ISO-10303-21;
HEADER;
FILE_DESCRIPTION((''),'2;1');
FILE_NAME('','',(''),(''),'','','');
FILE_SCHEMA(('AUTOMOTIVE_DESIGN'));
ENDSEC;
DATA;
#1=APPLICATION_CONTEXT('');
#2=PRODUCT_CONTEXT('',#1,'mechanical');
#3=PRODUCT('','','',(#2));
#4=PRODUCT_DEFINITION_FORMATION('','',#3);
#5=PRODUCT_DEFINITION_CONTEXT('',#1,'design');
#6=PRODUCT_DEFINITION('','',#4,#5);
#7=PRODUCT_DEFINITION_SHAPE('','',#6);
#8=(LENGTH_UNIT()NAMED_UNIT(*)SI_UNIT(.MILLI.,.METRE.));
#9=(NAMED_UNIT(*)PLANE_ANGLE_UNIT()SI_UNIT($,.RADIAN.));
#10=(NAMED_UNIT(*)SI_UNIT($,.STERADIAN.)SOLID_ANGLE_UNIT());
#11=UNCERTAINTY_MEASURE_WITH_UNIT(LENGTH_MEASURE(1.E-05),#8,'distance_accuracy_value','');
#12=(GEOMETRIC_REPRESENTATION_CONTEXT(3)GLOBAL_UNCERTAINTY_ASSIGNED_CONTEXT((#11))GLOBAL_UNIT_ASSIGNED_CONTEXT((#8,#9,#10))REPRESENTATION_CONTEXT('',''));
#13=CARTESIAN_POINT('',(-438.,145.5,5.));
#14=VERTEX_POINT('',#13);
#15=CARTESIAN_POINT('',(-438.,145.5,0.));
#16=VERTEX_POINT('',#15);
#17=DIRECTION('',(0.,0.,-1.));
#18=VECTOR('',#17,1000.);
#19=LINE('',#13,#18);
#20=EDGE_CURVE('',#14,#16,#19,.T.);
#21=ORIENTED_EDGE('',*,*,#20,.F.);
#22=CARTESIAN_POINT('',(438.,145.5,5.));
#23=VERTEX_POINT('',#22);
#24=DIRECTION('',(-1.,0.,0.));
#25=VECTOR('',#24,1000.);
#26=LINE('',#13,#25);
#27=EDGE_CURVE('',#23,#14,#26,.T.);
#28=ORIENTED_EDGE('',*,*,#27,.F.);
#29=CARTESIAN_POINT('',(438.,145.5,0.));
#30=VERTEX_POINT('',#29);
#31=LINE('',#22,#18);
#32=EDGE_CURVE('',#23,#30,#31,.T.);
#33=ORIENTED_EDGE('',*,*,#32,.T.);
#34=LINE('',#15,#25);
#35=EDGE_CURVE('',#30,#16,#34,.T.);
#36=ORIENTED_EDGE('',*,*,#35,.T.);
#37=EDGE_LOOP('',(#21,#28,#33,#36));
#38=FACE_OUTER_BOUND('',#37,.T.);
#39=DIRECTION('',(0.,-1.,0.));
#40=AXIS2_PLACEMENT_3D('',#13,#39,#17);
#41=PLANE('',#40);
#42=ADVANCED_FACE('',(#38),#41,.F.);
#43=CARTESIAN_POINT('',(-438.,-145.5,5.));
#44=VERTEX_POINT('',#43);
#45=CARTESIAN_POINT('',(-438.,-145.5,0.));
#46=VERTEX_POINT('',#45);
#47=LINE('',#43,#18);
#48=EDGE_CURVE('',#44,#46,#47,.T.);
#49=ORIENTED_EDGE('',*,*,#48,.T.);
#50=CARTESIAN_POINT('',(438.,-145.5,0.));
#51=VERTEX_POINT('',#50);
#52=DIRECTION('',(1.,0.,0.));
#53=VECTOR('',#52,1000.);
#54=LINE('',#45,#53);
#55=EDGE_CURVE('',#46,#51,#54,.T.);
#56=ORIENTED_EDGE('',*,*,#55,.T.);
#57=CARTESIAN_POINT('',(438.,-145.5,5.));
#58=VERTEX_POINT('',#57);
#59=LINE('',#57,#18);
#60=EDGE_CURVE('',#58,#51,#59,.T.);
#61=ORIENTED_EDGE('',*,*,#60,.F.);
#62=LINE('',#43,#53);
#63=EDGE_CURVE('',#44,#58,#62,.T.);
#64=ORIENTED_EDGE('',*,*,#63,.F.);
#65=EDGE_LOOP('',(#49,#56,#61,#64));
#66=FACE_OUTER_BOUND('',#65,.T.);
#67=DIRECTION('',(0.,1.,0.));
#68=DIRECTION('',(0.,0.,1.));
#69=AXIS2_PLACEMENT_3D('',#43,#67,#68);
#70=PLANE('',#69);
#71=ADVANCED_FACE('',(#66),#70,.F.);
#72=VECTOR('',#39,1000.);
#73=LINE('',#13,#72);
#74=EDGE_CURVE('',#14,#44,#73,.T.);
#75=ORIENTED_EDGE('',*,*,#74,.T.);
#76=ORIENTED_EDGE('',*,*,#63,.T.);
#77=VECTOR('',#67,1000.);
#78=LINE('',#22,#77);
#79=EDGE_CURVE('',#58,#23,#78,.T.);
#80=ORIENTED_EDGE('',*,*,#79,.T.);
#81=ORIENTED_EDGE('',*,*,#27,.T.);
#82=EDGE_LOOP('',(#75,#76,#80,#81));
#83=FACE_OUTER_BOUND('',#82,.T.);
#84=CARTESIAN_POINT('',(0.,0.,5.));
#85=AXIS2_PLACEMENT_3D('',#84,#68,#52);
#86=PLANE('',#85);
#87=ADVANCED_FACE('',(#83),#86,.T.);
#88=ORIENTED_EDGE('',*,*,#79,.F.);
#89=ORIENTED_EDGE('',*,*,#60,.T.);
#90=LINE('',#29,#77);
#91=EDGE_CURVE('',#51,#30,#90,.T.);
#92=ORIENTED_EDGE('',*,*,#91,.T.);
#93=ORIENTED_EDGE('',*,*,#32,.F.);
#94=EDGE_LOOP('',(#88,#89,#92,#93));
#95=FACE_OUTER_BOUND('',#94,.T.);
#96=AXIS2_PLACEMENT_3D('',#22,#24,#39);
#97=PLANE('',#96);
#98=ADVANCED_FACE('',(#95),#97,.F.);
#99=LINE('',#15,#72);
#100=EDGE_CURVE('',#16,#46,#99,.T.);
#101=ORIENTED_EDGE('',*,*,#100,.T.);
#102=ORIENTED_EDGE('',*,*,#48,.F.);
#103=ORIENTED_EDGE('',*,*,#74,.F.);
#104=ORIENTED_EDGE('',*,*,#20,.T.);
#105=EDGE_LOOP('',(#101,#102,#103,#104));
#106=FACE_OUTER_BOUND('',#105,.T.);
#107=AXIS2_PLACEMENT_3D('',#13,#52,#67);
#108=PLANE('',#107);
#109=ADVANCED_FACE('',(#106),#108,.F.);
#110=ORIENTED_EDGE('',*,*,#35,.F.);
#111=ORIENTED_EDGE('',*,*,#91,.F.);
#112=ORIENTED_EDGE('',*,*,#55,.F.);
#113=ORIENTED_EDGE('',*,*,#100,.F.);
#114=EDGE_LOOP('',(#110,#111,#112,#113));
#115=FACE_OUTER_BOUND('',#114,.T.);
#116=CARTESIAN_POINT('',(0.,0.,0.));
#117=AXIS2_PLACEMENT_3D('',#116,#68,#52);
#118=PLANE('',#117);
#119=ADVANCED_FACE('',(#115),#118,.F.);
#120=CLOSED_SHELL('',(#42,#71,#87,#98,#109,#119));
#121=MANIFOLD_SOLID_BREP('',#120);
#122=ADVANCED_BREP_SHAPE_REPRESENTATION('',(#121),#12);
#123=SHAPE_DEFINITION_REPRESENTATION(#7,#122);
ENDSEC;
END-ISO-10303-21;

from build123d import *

# Parameters (mm, degrees)
SKETCH_1_W      = 876
SKETCH_1_H      = 291
EXTRUDE_1_DEPTH = 5


with BuildPart() as part:
    # 草图1 → 凸台-拉伸1 (new body)
    with BuildSketch(Plane.XY):
        Rectangle(SKETCH_1_W, SKETCH_1_H)
    extrude(amount=EXTRUDE_1_DEPTH)


solid = part.part
